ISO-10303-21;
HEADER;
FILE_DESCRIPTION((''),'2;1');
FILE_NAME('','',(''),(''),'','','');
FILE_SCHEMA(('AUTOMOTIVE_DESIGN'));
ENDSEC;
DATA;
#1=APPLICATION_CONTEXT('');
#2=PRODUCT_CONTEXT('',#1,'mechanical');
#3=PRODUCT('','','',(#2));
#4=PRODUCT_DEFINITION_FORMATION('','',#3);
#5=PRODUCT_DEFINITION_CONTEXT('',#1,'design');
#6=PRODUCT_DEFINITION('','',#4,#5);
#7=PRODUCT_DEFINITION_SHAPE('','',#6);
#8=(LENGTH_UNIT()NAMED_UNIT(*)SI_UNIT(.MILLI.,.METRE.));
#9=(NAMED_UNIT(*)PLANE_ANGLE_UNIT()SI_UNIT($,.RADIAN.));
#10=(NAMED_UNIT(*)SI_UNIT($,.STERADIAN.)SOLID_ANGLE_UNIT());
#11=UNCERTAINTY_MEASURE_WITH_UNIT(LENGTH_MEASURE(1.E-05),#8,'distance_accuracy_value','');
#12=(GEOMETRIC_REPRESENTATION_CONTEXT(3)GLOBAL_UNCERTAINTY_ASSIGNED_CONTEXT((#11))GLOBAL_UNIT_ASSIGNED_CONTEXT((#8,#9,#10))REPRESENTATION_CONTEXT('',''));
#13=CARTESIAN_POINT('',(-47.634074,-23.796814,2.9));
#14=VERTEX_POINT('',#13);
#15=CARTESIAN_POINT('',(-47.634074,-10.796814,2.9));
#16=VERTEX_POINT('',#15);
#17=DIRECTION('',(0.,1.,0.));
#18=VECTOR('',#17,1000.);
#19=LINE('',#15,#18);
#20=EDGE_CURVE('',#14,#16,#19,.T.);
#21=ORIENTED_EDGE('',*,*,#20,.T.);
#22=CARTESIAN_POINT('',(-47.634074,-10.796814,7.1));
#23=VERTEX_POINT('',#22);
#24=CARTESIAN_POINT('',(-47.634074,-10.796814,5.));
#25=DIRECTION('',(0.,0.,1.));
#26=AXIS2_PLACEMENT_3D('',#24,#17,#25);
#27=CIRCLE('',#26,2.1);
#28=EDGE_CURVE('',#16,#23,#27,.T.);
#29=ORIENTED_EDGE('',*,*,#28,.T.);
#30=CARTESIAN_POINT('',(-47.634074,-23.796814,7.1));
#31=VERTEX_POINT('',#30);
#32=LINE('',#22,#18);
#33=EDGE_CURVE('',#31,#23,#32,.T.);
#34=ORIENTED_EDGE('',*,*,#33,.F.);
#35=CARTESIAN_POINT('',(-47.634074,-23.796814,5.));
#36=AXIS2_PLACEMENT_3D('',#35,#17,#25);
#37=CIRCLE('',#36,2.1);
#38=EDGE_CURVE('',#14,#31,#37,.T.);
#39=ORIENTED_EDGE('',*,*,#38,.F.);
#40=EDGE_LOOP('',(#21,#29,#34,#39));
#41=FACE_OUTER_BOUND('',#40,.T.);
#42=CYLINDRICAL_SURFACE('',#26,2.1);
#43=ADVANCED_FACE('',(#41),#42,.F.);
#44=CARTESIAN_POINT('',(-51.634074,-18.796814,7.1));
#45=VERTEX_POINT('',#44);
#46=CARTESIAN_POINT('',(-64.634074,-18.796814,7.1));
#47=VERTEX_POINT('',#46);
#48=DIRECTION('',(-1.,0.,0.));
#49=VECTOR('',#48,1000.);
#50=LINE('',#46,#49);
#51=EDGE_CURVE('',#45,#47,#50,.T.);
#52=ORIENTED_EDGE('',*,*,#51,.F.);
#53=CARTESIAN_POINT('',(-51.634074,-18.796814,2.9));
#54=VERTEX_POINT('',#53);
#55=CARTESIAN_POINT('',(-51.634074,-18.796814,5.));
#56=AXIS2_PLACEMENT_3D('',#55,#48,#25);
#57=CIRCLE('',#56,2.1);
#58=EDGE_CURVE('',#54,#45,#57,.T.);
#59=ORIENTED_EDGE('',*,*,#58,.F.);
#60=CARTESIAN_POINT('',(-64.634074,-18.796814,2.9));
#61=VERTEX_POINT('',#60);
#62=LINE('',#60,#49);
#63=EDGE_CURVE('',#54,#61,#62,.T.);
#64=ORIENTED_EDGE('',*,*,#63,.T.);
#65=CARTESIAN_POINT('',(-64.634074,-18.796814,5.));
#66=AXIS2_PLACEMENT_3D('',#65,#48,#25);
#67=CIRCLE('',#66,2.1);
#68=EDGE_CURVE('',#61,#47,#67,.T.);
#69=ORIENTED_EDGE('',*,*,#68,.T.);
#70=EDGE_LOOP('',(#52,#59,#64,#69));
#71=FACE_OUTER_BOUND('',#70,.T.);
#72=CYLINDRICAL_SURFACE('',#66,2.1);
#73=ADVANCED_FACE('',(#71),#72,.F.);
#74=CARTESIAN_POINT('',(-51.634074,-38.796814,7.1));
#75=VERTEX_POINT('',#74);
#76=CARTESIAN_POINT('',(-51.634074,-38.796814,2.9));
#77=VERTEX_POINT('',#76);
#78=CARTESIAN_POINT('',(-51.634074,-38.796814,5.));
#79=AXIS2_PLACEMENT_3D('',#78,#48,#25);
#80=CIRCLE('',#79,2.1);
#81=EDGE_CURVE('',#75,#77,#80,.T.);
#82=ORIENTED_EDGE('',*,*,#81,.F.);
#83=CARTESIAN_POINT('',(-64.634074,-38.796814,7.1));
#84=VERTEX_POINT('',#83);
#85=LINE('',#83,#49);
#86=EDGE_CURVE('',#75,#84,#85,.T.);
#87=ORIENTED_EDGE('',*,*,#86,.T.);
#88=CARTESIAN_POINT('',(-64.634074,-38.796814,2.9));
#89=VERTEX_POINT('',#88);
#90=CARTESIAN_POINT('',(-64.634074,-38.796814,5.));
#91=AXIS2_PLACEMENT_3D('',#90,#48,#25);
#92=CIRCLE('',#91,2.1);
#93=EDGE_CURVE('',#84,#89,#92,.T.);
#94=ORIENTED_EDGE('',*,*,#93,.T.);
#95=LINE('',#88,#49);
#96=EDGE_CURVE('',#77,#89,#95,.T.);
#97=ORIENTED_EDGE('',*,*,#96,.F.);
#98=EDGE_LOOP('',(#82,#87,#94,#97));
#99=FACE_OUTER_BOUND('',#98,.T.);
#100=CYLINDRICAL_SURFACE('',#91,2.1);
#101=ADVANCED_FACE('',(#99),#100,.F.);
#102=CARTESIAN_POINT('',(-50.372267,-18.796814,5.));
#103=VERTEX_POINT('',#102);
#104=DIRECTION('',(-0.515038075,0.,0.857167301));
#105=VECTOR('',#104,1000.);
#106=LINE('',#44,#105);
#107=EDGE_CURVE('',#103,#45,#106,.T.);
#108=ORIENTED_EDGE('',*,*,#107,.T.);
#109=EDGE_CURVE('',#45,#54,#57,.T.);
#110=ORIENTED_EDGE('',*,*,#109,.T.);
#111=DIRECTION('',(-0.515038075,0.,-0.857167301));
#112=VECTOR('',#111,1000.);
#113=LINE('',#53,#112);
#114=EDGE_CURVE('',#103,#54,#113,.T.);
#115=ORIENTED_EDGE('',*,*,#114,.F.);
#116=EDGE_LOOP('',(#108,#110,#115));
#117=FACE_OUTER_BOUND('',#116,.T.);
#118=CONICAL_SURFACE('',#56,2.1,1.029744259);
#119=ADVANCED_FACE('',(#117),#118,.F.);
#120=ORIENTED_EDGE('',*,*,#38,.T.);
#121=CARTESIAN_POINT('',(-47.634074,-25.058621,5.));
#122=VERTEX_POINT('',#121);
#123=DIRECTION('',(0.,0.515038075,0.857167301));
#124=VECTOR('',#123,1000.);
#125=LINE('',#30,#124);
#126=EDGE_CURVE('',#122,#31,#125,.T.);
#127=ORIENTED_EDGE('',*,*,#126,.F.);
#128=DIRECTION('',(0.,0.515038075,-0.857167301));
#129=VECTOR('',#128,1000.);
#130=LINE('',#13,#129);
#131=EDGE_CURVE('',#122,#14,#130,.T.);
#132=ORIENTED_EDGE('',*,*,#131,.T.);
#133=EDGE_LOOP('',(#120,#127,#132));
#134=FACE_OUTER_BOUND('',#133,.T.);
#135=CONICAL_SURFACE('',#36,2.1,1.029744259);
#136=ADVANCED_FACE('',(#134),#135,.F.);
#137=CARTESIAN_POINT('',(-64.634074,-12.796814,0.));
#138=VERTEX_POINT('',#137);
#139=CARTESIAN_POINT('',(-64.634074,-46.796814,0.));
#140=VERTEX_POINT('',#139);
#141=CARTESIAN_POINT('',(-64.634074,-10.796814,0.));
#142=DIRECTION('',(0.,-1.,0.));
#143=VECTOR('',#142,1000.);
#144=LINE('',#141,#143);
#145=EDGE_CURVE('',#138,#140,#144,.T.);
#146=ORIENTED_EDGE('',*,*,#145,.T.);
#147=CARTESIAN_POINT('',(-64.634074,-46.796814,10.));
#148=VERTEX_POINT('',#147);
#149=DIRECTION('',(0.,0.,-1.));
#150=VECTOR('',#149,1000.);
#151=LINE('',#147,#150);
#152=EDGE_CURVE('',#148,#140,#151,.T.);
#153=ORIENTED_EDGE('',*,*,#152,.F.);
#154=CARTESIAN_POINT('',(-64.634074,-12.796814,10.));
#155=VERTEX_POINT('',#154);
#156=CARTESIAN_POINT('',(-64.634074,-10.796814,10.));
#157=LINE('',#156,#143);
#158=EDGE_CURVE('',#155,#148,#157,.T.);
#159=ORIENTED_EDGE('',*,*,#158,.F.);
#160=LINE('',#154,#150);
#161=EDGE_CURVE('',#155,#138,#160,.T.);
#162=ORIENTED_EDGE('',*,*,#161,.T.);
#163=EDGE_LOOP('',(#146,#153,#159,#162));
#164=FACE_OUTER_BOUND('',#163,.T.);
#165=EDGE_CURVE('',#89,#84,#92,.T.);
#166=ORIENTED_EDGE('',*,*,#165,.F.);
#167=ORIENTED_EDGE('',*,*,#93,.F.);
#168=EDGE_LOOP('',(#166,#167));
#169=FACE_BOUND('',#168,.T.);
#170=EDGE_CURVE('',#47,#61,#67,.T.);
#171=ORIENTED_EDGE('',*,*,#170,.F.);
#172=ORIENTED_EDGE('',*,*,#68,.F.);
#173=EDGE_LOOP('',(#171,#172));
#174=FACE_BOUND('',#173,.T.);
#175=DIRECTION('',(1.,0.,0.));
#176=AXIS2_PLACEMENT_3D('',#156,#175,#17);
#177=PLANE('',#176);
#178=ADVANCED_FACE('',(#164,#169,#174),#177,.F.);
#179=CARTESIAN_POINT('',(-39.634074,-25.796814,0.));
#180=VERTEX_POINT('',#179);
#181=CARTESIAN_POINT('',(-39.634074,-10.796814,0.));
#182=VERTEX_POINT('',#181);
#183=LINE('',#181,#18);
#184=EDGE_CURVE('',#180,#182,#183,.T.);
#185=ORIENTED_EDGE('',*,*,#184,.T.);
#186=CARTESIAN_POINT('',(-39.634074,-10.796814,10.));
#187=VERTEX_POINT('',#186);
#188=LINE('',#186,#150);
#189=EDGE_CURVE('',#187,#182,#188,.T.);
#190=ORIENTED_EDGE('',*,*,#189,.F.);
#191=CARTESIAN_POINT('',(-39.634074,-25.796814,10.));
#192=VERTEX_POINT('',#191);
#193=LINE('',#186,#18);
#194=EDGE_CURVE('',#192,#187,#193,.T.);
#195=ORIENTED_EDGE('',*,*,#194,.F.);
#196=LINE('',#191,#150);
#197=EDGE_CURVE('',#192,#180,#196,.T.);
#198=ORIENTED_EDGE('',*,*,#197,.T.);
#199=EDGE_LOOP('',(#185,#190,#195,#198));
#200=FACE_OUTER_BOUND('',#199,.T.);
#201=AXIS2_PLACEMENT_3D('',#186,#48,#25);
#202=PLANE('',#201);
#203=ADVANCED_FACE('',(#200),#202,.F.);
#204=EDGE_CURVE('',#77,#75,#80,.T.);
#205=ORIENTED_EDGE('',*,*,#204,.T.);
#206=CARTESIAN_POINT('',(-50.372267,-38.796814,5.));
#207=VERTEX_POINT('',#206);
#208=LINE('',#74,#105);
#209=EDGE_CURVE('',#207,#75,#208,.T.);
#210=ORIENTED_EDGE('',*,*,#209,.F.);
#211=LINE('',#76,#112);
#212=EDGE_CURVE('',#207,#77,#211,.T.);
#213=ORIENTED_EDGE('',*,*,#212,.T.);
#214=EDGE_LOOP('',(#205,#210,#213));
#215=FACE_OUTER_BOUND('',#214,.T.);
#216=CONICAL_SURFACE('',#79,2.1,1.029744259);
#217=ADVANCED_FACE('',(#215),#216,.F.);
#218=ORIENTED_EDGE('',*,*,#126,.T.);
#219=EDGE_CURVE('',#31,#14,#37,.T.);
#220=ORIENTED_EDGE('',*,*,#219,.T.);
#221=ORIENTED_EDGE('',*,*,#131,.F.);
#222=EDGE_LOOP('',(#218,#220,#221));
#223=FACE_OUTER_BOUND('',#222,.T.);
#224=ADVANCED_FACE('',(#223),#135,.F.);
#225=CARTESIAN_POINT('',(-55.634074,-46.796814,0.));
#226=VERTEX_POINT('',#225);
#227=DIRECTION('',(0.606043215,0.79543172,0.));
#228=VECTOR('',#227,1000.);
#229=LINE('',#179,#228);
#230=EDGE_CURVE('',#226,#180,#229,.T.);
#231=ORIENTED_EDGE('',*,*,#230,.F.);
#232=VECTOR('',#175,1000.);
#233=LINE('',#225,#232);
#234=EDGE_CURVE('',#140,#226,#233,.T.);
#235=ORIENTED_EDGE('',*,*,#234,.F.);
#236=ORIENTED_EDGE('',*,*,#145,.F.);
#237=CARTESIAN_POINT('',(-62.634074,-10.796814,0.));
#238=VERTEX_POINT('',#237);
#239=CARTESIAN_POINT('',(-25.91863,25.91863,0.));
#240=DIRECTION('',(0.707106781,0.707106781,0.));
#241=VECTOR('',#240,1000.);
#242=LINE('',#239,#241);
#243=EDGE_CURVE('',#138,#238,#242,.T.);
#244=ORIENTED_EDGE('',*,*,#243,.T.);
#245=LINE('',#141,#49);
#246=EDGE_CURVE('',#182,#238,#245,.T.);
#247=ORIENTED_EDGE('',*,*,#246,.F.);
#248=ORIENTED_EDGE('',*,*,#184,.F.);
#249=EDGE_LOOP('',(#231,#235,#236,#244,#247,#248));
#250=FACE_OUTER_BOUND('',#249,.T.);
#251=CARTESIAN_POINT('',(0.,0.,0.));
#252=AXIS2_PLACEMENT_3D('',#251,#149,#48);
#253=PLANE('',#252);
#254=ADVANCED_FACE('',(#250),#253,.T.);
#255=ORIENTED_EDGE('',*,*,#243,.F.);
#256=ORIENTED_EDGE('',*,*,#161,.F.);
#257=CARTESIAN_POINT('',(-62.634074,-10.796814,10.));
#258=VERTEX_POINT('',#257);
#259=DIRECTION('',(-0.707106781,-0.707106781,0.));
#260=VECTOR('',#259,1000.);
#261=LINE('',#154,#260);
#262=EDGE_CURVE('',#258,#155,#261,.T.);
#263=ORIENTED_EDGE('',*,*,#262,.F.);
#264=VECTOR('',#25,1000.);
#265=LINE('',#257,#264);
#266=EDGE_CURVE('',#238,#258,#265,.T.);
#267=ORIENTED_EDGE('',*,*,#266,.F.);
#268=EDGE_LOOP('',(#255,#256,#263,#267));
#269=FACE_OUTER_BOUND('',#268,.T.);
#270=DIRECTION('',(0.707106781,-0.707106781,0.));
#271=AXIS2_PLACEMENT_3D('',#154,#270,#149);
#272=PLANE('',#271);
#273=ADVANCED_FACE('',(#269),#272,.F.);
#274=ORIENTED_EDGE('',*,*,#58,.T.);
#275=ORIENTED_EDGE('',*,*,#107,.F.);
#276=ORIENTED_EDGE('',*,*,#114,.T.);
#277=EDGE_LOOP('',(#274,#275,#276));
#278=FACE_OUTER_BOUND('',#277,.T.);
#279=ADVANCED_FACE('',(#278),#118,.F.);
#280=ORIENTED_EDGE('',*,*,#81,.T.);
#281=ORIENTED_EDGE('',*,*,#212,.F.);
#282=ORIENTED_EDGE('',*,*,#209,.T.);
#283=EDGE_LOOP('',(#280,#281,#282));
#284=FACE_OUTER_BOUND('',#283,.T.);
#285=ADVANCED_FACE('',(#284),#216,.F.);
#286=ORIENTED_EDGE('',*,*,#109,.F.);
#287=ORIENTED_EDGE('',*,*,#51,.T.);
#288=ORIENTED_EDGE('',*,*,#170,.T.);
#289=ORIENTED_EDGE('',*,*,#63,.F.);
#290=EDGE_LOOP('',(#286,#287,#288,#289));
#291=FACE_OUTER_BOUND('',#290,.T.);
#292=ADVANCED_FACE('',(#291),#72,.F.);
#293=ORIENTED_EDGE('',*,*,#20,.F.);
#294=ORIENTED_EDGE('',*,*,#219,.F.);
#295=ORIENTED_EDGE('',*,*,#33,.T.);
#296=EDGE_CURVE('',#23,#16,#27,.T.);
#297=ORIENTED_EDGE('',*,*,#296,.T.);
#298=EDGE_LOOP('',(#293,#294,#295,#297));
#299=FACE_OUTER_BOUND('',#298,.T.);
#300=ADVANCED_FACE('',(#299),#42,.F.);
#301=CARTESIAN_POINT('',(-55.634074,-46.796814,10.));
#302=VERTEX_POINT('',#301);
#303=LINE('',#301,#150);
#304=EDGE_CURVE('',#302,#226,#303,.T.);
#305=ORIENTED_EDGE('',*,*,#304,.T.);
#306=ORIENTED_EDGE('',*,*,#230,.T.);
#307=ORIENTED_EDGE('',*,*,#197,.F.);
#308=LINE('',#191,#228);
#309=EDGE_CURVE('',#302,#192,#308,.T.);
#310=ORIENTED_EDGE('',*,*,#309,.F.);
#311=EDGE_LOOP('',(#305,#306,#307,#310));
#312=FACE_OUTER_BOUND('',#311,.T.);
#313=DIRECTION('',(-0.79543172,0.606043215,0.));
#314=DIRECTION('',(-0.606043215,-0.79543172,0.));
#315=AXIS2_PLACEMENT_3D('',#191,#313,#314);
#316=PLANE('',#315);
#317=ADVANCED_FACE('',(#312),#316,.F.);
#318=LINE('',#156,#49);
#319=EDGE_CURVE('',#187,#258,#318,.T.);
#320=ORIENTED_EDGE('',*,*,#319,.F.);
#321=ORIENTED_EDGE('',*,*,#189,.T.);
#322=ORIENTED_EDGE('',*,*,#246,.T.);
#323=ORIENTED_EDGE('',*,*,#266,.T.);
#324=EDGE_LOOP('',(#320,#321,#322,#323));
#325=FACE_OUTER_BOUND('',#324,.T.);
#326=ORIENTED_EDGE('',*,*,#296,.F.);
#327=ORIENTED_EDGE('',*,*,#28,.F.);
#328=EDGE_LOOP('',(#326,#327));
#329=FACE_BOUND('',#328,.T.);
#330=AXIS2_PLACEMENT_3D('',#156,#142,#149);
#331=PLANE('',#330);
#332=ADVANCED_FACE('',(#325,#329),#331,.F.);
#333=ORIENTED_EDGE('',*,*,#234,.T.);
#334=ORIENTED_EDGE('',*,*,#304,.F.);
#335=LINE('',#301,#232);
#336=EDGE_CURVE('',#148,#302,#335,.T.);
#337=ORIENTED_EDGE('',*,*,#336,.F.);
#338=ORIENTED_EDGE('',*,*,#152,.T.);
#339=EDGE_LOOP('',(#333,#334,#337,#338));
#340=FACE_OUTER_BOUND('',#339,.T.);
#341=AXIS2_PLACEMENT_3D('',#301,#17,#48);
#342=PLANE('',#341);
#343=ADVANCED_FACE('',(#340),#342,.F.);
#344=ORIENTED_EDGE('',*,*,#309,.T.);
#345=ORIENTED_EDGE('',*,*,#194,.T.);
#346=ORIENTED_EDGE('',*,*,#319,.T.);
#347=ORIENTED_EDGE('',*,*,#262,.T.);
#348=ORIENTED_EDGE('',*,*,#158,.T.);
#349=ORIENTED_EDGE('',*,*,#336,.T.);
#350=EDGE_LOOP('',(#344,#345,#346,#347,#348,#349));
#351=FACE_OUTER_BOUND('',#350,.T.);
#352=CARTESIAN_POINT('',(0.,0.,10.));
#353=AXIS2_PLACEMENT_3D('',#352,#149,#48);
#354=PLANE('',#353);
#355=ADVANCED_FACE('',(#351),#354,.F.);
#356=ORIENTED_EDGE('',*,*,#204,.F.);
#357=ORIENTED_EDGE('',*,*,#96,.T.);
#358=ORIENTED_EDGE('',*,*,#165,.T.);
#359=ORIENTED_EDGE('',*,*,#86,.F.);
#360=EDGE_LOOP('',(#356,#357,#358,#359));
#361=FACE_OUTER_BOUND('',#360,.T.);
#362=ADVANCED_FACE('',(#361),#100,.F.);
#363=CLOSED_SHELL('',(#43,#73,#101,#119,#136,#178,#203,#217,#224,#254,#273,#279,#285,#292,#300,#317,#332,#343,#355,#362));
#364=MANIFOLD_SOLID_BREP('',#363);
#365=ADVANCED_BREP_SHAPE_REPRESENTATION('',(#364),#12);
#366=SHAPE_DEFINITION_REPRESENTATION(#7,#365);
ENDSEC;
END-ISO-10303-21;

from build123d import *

# Parameters (mm, degrees)
EXTRUDE_1_DEPTH        = 10
HOLE_WIZARD_M5_2_D     = 4.2
HOLE_WIZARD_M5_2_DEPTH = 13
HOLE_WIZARD_M5_2_TIP   = 1.2618073
HOLE_WIZARD_M5_1_D     = 4.2
HOLE_WIZARD_M5_1_DEPTH = 13
HOLE_WIZARD_M5_1_TIP   = 1.2618073
CHAMFER_1_SIZE         = 2


with BuildPart() as part:
    # 草图1 → 凸台-拉伸1 (new body)
    with BuildSketch(Plane.XY):
        Polygon((-64.634074155, -10.796814071), (-39.634074155, -10.796814071), (-39.634074155, -25.796814071), (-55.634074155, -46.796814071), (-64.634074155, -46.796814071), align=None)
    extrude(amount=EXTRUDE_1_DEPTH)

    # M5 螺纹孔2
    with Locations(Plane(origin=(0, -10.796814071, 0), x_dir=(1, 0, 0), z_dir=(0, 1, 0))):
        with Locations((-47.634074155, -5)):
            Hole(HOLE_WIZARD_M5_2_D / 2, depth=HOLE_WIZARD_M5_2_DEPTH)
            with Locations((0, 0, -(HOLE_WIZARD_M5_2_DEPTH + HOLE_WIZARD_M5_2_TIP / 2))):  # 118° drill point
                Cone(0, HOLE_WIZARD_M5_2_D / 2, HOLE_WIZARD_M5_2_TIP, mode=Mode.SUBTRACT)

    # M5 螺纹孔1
    with Locations(Plane.ZY.offset(64.634074155)):
        with Locations((5, -18.796814071), (5, -38.796814071)):
            Hole(HOLE_WIZARD_M5_1_D / 2, depth=HOLE_WIZARD_M5_1_DEPTH)
            with Locations((0, 0, -(HOLE_WIZARD_M5_1_DEPTH + HOLE_WIZARD_M5_1_TIP / 2))):  # 118° drill point
                Cone(0, HOLE_WIZARD_M5_1_D / 2, HOLE_WIZARD_M5_1_TIP, mode=Mode.SUBTRACT)

    # 倒角1
    chamfer_1_edges = [part.edges().sort_by_distance(p)[0] for p in [
        (-64.634074155, -10.796814071, 5),
    ]]
    chamfer(chamfer_1_edges, length=CHAMFER_1_SIZE)


solid = part.part
